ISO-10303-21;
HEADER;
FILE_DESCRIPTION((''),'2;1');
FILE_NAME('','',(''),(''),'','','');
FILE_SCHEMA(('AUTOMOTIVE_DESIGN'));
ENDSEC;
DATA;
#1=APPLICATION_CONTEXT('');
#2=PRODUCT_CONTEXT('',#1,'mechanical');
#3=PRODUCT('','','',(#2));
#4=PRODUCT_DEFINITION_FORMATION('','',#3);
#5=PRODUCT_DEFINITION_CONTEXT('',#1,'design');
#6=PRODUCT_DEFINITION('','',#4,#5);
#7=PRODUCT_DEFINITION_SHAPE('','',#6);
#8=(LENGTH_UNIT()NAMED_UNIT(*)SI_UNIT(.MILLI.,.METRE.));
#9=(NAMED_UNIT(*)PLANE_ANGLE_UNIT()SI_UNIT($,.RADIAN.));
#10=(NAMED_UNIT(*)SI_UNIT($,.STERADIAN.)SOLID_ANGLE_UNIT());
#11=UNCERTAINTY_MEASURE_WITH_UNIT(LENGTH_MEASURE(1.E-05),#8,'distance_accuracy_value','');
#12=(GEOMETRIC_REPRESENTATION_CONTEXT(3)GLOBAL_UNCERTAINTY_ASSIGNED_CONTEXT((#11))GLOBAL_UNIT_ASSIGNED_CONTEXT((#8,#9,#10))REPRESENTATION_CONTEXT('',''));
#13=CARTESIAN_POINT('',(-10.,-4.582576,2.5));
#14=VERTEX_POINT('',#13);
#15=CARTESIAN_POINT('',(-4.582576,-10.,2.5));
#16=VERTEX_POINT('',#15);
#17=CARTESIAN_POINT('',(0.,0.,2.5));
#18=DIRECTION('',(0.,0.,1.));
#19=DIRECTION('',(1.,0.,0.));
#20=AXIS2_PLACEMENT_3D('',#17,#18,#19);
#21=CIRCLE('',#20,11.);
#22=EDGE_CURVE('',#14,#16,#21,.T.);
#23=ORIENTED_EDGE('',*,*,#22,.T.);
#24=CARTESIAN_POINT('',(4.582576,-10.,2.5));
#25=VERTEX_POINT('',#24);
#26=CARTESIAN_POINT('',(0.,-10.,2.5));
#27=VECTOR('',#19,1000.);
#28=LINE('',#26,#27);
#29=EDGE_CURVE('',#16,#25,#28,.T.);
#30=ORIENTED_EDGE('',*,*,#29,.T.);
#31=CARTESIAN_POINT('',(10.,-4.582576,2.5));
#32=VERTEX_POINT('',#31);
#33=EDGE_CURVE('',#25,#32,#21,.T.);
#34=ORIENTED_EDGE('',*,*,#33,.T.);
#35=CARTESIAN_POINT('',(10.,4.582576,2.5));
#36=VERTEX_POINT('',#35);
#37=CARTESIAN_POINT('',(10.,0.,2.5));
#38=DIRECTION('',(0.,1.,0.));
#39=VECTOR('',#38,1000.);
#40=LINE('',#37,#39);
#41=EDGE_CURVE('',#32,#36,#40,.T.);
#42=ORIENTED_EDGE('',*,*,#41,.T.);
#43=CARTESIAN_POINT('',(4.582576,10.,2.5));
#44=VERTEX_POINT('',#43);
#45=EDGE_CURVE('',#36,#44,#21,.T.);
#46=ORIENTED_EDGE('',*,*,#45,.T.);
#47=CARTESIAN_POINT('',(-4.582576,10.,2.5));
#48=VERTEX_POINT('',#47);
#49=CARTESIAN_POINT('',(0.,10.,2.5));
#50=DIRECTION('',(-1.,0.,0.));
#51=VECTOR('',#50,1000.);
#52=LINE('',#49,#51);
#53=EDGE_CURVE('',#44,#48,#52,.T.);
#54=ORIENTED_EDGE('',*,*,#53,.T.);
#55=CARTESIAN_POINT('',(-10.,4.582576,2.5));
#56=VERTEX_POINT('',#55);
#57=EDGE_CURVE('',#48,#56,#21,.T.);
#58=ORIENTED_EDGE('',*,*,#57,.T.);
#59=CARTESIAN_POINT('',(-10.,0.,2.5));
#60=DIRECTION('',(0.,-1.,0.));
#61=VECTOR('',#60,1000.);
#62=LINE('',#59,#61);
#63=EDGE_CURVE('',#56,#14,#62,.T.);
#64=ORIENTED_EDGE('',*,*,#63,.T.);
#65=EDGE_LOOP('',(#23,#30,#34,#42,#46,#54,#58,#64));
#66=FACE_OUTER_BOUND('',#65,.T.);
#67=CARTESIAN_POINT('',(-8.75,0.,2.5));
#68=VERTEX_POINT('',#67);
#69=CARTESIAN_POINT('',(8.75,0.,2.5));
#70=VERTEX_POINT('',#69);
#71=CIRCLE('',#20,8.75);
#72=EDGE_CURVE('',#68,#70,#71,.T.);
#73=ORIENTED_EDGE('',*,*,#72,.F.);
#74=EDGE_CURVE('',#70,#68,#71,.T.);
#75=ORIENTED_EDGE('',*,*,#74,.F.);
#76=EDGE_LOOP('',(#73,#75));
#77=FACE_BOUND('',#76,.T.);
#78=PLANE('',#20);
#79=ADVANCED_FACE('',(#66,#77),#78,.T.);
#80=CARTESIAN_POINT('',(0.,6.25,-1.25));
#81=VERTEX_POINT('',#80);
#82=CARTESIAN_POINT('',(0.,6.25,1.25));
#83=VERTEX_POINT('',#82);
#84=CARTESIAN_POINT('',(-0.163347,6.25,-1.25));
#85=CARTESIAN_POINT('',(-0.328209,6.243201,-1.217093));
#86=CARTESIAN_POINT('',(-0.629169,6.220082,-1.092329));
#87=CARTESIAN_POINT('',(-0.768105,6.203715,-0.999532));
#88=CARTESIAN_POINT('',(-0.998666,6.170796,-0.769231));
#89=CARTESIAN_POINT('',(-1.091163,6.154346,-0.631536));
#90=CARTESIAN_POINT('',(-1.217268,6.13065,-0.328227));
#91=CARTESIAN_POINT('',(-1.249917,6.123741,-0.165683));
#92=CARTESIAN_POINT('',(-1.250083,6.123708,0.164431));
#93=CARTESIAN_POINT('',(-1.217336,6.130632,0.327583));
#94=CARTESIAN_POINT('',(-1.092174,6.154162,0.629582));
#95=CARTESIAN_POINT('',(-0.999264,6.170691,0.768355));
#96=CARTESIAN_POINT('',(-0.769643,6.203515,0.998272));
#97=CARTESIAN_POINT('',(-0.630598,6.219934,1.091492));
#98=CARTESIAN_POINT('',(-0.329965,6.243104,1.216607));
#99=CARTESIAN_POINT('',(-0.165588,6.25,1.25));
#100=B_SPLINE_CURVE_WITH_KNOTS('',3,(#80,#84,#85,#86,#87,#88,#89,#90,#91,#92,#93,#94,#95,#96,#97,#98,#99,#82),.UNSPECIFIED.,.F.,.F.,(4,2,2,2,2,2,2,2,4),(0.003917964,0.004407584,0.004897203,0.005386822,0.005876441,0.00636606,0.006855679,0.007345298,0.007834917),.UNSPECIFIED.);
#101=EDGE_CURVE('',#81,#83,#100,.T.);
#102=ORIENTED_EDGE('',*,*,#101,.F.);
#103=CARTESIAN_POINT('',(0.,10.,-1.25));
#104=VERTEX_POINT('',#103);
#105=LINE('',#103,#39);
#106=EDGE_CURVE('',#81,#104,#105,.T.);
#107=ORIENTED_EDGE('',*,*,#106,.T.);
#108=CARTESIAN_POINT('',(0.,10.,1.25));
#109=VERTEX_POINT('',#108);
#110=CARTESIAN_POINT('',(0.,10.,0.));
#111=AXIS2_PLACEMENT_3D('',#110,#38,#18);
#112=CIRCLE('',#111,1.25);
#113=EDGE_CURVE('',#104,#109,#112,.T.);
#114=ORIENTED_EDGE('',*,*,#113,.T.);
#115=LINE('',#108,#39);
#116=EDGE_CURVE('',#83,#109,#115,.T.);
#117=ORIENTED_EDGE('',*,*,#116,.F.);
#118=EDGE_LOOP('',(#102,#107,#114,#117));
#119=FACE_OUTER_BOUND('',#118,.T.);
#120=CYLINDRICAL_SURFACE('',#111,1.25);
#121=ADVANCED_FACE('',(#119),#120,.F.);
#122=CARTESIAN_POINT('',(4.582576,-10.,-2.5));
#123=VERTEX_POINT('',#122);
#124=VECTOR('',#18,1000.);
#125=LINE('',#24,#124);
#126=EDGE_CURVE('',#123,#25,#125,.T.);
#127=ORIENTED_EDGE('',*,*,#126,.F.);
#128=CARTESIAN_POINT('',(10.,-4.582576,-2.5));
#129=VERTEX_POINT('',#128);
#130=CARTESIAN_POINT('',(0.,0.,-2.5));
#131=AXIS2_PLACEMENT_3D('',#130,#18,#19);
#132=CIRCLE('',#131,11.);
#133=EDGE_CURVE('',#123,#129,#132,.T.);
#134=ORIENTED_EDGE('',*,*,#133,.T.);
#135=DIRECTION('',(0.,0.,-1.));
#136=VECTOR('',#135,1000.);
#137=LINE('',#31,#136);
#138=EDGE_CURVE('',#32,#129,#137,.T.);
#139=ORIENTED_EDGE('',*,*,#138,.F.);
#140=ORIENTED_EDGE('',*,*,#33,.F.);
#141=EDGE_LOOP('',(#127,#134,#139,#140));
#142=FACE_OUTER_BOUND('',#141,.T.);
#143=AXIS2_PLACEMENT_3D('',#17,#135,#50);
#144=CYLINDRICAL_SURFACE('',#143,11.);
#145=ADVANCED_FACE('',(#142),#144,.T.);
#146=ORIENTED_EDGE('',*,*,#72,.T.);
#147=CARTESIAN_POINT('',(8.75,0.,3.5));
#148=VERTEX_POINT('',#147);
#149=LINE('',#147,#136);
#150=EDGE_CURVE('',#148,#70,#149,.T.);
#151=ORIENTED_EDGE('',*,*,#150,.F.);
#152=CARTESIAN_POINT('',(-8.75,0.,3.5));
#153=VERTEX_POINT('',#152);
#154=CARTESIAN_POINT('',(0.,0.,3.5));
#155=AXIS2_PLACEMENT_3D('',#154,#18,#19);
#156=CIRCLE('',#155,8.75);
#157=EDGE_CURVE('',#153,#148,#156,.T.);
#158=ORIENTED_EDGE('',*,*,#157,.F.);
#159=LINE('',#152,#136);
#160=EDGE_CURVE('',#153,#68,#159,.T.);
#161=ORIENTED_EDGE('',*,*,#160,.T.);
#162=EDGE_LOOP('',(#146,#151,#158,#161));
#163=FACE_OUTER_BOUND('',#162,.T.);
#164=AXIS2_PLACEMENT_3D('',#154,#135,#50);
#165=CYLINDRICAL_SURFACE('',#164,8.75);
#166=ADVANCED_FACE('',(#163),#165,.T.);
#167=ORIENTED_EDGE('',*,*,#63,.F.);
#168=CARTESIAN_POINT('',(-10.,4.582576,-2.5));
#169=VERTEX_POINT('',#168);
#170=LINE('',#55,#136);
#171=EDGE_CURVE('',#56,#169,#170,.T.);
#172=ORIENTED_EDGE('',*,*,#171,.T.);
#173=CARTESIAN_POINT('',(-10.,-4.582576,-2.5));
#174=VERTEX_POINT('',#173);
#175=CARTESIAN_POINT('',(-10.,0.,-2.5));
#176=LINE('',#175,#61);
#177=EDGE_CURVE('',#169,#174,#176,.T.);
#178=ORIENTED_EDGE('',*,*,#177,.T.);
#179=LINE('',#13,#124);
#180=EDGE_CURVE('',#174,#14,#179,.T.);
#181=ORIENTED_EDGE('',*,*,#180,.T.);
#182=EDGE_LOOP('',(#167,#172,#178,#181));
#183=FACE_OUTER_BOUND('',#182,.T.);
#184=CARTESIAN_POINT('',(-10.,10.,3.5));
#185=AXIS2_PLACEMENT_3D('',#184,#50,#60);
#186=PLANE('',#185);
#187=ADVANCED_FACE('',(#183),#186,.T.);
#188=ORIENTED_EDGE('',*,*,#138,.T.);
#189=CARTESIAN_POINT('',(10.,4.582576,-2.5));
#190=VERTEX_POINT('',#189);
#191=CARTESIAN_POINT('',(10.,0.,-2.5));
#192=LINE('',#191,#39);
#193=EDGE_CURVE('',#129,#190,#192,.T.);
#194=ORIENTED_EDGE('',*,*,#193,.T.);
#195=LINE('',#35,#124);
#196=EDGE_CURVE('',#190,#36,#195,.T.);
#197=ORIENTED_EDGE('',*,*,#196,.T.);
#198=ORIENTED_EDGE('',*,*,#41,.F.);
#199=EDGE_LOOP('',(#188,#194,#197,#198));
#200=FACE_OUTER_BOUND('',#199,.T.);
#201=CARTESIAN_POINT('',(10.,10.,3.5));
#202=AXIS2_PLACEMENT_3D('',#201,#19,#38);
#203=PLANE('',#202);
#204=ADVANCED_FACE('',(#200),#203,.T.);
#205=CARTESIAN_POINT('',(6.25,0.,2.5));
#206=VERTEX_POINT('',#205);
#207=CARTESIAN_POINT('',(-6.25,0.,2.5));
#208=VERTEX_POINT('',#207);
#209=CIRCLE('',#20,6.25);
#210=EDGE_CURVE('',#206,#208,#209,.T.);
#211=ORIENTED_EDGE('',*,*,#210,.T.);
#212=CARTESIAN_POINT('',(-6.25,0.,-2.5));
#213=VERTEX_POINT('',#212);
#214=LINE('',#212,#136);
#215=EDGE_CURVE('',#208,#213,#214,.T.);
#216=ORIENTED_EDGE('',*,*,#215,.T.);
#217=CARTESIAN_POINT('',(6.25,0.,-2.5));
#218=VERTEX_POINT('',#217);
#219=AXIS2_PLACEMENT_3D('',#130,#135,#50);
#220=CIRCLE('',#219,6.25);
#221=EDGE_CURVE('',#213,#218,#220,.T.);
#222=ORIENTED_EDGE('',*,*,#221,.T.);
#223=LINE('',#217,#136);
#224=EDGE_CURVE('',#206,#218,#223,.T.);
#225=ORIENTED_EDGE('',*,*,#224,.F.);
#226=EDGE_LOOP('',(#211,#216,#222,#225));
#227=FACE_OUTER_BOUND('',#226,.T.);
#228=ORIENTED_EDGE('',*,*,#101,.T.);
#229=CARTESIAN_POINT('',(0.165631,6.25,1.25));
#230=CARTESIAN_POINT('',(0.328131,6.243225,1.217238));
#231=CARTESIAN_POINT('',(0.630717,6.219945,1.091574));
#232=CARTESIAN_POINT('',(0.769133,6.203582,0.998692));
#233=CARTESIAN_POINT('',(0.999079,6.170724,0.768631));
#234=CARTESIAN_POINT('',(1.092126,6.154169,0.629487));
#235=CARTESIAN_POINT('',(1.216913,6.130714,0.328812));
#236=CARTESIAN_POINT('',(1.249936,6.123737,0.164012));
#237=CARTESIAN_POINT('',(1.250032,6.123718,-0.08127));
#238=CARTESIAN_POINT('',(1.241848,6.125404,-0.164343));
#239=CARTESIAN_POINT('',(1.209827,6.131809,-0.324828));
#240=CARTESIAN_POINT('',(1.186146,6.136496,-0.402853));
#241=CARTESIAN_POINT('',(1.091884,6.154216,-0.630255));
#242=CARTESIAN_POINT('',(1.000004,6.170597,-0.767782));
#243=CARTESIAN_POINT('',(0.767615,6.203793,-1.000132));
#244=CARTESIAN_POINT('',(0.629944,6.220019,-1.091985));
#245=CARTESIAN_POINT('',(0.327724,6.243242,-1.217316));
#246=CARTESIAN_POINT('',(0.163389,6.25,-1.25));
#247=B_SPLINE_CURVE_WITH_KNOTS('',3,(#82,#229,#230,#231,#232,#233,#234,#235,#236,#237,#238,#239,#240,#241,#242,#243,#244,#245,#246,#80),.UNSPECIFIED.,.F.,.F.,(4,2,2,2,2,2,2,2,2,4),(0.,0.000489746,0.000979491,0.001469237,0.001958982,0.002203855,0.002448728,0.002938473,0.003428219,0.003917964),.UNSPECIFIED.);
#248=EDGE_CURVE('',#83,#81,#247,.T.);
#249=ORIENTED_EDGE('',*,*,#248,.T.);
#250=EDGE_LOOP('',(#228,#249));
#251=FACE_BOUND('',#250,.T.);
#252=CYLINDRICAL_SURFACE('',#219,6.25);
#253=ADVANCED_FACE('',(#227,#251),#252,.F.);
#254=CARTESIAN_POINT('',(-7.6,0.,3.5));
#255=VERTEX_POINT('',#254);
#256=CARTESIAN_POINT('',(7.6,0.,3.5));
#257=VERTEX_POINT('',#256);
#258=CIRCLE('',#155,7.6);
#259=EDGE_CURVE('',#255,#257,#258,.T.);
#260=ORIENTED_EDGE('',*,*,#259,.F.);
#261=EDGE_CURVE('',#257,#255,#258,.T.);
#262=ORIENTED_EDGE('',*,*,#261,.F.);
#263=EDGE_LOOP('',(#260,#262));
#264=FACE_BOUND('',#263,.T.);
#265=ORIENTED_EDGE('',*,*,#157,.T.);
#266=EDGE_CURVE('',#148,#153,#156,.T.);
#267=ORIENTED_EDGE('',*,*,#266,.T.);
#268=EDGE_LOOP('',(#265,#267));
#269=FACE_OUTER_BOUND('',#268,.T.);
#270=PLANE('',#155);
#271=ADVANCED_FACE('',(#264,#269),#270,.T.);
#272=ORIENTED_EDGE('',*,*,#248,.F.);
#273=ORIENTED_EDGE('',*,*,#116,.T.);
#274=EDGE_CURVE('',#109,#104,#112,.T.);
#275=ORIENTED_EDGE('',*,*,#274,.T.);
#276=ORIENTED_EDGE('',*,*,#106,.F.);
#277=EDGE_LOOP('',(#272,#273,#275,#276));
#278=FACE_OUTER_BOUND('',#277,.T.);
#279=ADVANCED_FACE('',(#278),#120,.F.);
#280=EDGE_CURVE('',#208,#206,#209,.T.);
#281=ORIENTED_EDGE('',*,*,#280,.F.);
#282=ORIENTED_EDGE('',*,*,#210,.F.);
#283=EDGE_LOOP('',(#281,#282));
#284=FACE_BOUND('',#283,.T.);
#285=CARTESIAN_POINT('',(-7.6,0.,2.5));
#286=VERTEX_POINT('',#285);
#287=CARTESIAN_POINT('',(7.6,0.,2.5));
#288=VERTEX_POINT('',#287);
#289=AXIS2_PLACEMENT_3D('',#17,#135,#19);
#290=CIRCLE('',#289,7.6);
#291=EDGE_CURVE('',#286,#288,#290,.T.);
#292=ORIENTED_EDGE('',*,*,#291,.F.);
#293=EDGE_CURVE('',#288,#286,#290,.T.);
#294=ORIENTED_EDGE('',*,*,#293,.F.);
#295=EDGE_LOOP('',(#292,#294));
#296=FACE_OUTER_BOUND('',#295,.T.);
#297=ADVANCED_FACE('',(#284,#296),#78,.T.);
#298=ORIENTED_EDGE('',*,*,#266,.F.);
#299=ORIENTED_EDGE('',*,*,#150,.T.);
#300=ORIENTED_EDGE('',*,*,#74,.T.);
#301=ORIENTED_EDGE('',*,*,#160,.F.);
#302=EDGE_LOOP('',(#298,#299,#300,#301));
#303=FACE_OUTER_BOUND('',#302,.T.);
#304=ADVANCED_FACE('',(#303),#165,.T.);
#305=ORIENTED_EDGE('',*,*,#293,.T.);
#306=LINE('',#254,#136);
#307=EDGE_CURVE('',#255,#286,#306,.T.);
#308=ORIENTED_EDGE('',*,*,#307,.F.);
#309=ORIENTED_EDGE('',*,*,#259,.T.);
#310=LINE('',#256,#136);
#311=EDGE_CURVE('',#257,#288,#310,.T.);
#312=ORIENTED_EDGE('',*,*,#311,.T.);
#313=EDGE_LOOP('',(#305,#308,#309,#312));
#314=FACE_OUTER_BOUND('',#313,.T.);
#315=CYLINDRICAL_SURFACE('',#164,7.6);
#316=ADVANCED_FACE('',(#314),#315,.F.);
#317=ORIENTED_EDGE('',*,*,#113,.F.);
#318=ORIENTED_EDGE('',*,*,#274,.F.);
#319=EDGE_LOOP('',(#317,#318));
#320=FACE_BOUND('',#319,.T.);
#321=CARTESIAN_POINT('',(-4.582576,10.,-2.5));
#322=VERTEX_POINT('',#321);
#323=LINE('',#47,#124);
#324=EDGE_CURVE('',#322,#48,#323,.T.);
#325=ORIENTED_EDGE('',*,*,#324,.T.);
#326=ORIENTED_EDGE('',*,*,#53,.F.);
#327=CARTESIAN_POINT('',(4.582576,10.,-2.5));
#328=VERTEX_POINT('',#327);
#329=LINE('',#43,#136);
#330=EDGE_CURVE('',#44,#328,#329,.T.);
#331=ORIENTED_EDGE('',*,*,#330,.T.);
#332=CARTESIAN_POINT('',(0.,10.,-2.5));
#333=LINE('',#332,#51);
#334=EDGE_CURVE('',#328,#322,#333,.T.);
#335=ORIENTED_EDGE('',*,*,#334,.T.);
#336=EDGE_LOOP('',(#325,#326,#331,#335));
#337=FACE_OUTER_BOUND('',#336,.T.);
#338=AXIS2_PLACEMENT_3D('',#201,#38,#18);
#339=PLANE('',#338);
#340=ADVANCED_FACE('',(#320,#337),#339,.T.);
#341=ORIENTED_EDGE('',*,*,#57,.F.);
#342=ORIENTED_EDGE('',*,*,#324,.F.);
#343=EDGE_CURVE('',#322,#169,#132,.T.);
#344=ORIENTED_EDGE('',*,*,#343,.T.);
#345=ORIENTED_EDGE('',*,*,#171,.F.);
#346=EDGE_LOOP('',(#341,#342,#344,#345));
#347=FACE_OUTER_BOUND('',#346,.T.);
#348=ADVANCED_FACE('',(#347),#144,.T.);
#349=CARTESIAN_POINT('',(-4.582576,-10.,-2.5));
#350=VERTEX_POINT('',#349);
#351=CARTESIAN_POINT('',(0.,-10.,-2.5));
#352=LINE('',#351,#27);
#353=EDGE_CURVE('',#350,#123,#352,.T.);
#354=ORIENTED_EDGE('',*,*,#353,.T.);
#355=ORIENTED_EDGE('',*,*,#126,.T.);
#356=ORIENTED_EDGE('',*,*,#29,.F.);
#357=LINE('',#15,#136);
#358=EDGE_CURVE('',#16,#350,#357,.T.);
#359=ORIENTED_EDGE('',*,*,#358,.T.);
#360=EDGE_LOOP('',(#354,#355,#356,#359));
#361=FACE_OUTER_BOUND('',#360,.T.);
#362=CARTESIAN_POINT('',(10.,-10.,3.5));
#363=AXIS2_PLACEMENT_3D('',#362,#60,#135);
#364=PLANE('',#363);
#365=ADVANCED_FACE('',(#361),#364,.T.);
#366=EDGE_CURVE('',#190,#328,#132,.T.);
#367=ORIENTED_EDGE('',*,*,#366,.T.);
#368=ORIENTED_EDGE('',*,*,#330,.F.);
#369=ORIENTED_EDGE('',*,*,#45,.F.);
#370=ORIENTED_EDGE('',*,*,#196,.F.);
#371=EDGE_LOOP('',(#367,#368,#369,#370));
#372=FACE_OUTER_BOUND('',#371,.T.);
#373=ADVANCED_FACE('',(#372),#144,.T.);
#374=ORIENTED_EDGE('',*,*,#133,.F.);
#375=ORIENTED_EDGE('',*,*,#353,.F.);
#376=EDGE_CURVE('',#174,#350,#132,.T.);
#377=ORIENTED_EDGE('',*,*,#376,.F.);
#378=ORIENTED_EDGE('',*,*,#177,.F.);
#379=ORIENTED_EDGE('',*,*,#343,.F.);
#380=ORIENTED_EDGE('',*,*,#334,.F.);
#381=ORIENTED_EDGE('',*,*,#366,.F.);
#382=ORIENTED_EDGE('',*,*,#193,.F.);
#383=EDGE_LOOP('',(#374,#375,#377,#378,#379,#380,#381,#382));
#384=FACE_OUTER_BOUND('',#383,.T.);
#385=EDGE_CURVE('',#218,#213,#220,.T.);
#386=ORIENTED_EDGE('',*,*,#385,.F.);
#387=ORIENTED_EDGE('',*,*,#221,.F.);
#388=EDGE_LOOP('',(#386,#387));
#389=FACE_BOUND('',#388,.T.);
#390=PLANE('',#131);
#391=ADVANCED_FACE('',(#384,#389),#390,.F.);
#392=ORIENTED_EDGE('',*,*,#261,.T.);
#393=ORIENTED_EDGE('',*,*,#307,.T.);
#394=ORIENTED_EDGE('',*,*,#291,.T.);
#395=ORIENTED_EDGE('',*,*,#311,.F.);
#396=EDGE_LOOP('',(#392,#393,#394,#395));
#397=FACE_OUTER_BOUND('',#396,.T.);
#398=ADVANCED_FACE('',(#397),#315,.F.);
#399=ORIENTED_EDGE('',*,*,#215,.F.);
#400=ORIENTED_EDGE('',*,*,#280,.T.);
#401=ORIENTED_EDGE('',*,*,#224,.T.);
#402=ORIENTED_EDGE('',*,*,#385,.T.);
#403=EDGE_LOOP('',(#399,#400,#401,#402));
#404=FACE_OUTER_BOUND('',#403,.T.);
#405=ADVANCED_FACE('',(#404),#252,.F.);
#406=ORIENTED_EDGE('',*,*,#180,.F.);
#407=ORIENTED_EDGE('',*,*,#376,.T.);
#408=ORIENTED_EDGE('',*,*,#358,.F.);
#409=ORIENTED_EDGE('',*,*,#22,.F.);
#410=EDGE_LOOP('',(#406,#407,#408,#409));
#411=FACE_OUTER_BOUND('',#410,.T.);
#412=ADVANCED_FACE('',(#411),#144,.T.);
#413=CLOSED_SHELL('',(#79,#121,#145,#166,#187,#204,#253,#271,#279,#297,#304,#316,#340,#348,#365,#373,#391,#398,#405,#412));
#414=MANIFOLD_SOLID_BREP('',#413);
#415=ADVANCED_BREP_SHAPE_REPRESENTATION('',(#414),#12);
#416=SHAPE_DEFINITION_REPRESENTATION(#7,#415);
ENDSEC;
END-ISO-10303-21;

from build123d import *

# Parameters (mm, degrees)
SKETCH7_R              = 11
BOSS_EXTRUDE1_DEPTH    = 2.5
SKETCH8_R              = 8.75
SKETCH8_R_2            = 7.6
BOSS_EXTRUDE2_DEPTH    = 1
M14X1_5_TAPPED_HOLE1_D = 12.5
SKETCH13_OUTSIDE_W     = 30.338
SKETCH13_OUTSIDE_H     = 30.338
SKETCH13_OUTSIDE_W_2   = 20
SKETCH13_OUTSIDE_H_2   = 20
CUT_EXTRUDE1_DEPTH     = 17.673332001
M3_TAPPED_HOLE3_REACH  = 24.633
M3_TAPPED_HOLE3_BORE_R = 1.25


with BuildPart() as part:
    # Sketch7 → Boss-Extrude1 (new, symmetric)
    with BuildSketch(Plane.XY):
        Circle(SKETCH7_R)
    extrude(amount=BOSS_EXTRUDE1_DEPTH, both=True)

    # Sketch8 → Boss-Extrude2 (add)
    with BuildSketch(Plane.XY.offset(2.5)):
        Circle(SKETCH8_R)
        Circle(SKETCH8_R_2, mode=Mode.SUBTRACT)
    extrude(amount=BOSS_EXTRUDE2_DEPTH)

    # M14x1.5 Tapped Hole1 (through all)
    with Locations(Plane(origin=(0, 0, -2.5), x_dir=(-1, 0, 0), z_dir=(0, 0, -1))):
        with Locations((0, 0)):
            Hole(M14X1_5_TAPPED_HOLE1_D / 2)

    # Sketch13 outside → Cut-Extrude1 (cut, through all)
    with BuildSketch(Plane(origin=(0, 0, -2.5), x_dir=(-1, 0, 0), z_dir=(0, 0, -1))):
        Rectangle(SKETCH13_OUTSIDE_W, SKETCH13_OUTSIDE_H)
        Rectangle(SKETCH13_OUTSIDE_W_2, SKETCH13_OUTSIDE_H_2, mode=Mode.SUBTRACT)
    extrude(amount=-CUT_EXTRUDE1_DEPTH, mode=Mode.SUBTRACT)

    # M3 Tapped Hole3 bore → M3 Tapped Hole3 (cut, up to next)
    with BuildSketch(Plane(origin=(0, 10, 0), x_dir=(1, 0, 0), z_dir=(0, 1, 0)), mode=Mode.PRIVATE) as m3_tapped_hole3_sk1:
        Circle(M3_TAPPED_HOLE3_BORE_R)
    m3_tapped_hole3_tool1 = extrude(m3_tapped_hole3_sk1.sketch, amount=-M3_TAPPED_HOLE3_REACH, mode=Mode.PRIVATE) & part.part
    add(m3_tapped_hole3_tool1.solids().sort_by_distance((0, 10, 0))[0], mode=Mode.SUBTRACT)


solid = part.part
